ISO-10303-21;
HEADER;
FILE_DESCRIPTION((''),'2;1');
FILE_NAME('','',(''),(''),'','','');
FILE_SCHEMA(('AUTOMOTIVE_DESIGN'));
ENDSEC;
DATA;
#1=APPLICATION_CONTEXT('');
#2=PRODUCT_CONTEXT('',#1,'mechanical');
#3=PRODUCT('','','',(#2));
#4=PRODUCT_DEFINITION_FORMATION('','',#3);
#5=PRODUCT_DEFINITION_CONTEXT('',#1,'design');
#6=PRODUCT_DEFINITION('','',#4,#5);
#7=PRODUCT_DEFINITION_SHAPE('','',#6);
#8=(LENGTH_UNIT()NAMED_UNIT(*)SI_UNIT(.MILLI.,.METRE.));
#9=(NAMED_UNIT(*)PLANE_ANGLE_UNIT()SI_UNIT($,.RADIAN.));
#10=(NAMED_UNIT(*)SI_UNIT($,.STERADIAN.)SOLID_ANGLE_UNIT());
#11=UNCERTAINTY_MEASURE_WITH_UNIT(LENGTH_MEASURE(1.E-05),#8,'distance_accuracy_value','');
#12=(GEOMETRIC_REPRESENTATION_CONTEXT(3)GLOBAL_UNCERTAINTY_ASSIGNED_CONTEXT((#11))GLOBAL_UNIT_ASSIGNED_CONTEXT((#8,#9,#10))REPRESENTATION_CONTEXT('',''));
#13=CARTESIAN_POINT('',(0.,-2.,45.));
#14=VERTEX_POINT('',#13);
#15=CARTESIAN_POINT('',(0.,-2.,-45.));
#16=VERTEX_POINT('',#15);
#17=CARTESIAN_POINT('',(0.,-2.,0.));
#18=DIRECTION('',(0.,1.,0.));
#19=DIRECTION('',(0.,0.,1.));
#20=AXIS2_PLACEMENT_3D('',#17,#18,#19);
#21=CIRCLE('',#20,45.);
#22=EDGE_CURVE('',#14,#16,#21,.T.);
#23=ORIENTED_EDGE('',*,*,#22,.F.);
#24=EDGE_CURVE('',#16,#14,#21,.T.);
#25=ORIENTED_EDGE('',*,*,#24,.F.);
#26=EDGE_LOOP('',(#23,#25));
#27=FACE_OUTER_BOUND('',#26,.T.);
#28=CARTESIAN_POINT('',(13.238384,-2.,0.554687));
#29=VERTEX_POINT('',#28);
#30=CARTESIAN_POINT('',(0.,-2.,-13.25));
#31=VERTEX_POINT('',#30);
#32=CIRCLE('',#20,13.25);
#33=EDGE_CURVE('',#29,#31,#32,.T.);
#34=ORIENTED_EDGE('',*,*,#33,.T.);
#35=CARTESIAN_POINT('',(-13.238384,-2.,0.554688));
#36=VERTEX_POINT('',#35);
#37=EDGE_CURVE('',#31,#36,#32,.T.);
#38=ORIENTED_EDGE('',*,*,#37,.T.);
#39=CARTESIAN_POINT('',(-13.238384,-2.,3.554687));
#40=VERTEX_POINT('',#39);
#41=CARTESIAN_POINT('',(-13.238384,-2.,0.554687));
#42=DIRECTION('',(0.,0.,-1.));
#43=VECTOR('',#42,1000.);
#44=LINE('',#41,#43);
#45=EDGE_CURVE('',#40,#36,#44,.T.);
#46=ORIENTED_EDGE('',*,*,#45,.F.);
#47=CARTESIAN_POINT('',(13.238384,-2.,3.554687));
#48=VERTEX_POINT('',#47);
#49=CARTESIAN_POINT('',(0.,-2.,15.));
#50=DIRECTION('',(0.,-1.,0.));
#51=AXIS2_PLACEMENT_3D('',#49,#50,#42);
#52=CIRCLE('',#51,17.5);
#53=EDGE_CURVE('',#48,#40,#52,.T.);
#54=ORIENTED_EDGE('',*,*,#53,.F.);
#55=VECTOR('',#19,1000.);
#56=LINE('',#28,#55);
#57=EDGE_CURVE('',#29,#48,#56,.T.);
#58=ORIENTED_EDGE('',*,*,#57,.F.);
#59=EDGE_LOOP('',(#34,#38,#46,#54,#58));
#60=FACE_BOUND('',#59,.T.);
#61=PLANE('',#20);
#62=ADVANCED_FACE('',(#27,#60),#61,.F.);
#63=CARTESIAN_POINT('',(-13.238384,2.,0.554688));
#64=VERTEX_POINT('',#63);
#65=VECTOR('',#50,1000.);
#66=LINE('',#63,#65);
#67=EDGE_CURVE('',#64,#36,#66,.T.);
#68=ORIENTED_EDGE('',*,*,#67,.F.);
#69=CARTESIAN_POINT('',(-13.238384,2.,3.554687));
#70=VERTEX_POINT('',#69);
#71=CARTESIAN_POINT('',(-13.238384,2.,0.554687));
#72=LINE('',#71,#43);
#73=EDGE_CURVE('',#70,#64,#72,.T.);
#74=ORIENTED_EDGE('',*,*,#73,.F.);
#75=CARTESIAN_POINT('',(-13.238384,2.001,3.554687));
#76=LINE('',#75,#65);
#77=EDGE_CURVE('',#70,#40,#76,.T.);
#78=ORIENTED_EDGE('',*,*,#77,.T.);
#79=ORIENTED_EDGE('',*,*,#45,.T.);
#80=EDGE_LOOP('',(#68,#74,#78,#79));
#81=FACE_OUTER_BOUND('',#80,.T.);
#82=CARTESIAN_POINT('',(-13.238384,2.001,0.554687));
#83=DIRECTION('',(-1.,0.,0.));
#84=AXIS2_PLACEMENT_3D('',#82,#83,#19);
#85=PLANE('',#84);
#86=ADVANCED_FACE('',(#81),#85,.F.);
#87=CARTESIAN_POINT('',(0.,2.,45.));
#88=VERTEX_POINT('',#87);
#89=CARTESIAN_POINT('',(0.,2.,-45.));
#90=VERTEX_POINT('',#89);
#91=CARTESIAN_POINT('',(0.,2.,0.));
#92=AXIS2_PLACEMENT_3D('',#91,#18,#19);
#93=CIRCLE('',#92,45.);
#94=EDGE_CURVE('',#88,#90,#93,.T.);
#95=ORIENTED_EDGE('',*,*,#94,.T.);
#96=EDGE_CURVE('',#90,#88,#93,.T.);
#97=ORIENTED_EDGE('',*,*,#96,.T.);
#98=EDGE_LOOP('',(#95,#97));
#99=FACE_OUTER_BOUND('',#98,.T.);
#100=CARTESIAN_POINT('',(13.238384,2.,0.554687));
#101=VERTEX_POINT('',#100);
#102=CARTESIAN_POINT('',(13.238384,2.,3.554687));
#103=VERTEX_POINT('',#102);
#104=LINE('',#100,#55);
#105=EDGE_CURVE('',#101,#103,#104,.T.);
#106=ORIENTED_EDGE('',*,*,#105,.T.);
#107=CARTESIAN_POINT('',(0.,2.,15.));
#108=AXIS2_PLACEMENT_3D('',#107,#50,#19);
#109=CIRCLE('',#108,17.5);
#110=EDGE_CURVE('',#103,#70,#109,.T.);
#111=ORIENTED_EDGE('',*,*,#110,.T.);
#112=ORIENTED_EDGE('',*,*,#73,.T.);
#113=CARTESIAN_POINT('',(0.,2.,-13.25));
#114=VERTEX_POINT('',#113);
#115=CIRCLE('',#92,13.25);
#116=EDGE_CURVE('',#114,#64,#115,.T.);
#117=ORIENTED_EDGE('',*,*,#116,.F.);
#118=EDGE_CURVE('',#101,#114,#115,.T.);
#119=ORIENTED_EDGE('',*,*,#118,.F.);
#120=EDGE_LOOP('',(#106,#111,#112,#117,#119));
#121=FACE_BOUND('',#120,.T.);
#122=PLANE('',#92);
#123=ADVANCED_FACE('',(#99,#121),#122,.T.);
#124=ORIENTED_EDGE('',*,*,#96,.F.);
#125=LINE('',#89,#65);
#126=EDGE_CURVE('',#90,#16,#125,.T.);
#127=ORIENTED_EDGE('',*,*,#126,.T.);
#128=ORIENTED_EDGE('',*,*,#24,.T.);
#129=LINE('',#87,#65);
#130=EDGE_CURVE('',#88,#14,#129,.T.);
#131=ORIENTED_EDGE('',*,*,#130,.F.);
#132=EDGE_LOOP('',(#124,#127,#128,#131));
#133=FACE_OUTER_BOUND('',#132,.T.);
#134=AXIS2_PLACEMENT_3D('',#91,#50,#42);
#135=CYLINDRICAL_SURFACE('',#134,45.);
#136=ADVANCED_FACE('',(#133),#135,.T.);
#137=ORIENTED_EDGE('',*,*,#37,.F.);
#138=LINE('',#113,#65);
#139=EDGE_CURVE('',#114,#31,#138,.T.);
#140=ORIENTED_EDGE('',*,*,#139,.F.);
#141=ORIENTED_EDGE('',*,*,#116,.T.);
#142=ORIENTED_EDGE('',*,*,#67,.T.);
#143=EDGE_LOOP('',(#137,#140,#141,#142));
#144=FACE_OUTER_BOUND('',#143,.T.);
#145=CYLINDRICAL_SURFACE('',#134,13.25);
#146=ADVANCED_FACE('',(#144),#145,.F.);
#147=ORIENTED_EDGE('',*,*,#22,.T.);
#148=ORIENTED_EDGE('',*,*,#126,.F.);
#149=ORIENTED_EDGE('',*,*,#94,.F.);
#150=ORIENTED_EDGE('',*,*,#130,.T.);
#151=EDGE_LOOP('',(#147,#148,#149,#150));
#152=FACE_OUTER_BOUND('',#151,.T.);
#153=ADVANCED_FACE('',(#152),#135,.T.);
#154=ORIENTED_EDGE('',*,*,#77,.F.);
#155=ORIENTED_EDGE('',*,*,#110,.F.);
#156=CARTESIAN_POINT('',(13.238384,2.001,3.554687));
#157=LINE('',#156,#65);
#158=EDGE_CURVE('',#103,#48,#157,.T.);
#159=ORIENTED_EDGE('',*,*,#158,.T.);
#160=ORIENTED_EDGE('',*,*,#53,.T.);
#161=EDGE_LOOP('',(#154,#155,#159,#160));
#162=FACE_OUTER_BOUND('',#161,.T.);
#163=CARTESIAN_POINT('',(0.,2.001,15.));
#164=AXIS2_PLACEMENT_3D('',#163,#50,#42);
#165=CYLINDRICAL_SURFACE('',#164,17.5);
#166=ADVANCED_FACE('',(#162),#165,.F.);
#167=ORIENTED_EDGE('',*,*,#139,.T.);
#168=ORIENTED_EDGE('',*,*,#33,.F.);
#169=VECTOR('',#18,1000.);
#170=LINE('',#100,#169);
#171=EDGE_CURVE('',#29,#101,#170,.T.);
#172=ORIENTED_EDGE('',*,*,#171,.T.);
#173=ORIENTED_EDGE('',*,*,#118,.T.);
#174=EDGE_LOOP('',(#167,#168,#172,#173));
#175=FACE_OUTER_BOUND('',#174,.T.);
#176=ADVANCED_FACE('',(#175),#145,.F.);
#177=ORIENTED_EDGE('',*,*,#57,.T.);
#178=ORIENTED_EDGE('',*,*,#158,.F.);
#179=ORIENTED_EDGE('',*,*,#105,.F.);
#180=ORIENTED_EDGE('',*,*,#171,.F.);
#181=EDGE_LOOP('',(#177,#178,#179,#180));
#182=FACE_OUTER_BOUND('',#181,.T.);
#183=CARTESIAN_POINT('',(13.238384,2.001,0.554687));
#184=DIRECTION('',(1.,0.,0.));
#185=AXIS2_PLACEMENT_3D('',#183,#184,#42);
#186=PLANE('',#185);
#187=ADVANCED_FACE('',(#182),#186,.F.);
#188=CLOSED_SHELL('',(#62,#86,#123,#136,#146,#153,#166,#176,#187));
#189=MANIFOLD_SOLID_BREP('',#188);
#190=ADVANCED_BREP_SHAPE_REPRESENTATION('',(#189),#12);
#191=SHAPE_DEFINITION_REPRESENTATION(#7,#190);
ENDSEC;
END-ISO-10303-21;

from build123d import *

# Parameters (mm, degrees)
SKETCH_1_R          = 45
SKETCH_1_R_2        = 13.25
EXTRUDE_1_DEPTH     = 2
CUT_EXTRUDE_1_REACH = 65.765


with BuildPart() as part:
    # 草图1 → 凸台-拉伸1 (new, symmetric)
    with BuildSketch(Plane(origin=(0, 0, 0), x_dir=(1, 0, 0), z_dir=(0, 1, 0))):
        with Locations(Location((0, 0, 0), (0, 0, 270))):
            Circle(SKETCH_1_R)
        with Locations(Location((0, 0, 0), (0, 0, 270))):
            Circle(SKETCH_1_R_2, mode=Mode.SUBTRACT)
    extrude(amount=EXTRUDE_1_DEPTH, both=True)

    # 草图2 → 切除-拉伸1 (cut, up to next)
    with BuildSketch(Plane.XZ.offset(2), mode=Mode.PRIVATE) as cut_extrude_1_sk1:
        with BuildLine():
            Line((-13.23838441, 0.5546875), (-13.23838441, 3.5546875))
            ThreePointArc((-13.23838441, 3.5546875), (0, 32.5), (13.23838441, 3.5546875))
            Line((13.23838441, 3.5546875), (13.23838441, 0.5546875))
            Line((13.23838441, 0.5546875), (-13.23838441, 0.5546875))
        make_face()
    cut_extrude_1_tool1 = extrude(cut_extrude_1_sk1.sketch, amount=-CUT_EXTRUDE_1_REACH, mode=Mode.PRIVATE) & part.part
    add(cut_extrude_1_tool1.solids().sort_by_distance((0, -2, 15.557308))[0], mode=Mode.SUBTRACT)


solid = part.part
